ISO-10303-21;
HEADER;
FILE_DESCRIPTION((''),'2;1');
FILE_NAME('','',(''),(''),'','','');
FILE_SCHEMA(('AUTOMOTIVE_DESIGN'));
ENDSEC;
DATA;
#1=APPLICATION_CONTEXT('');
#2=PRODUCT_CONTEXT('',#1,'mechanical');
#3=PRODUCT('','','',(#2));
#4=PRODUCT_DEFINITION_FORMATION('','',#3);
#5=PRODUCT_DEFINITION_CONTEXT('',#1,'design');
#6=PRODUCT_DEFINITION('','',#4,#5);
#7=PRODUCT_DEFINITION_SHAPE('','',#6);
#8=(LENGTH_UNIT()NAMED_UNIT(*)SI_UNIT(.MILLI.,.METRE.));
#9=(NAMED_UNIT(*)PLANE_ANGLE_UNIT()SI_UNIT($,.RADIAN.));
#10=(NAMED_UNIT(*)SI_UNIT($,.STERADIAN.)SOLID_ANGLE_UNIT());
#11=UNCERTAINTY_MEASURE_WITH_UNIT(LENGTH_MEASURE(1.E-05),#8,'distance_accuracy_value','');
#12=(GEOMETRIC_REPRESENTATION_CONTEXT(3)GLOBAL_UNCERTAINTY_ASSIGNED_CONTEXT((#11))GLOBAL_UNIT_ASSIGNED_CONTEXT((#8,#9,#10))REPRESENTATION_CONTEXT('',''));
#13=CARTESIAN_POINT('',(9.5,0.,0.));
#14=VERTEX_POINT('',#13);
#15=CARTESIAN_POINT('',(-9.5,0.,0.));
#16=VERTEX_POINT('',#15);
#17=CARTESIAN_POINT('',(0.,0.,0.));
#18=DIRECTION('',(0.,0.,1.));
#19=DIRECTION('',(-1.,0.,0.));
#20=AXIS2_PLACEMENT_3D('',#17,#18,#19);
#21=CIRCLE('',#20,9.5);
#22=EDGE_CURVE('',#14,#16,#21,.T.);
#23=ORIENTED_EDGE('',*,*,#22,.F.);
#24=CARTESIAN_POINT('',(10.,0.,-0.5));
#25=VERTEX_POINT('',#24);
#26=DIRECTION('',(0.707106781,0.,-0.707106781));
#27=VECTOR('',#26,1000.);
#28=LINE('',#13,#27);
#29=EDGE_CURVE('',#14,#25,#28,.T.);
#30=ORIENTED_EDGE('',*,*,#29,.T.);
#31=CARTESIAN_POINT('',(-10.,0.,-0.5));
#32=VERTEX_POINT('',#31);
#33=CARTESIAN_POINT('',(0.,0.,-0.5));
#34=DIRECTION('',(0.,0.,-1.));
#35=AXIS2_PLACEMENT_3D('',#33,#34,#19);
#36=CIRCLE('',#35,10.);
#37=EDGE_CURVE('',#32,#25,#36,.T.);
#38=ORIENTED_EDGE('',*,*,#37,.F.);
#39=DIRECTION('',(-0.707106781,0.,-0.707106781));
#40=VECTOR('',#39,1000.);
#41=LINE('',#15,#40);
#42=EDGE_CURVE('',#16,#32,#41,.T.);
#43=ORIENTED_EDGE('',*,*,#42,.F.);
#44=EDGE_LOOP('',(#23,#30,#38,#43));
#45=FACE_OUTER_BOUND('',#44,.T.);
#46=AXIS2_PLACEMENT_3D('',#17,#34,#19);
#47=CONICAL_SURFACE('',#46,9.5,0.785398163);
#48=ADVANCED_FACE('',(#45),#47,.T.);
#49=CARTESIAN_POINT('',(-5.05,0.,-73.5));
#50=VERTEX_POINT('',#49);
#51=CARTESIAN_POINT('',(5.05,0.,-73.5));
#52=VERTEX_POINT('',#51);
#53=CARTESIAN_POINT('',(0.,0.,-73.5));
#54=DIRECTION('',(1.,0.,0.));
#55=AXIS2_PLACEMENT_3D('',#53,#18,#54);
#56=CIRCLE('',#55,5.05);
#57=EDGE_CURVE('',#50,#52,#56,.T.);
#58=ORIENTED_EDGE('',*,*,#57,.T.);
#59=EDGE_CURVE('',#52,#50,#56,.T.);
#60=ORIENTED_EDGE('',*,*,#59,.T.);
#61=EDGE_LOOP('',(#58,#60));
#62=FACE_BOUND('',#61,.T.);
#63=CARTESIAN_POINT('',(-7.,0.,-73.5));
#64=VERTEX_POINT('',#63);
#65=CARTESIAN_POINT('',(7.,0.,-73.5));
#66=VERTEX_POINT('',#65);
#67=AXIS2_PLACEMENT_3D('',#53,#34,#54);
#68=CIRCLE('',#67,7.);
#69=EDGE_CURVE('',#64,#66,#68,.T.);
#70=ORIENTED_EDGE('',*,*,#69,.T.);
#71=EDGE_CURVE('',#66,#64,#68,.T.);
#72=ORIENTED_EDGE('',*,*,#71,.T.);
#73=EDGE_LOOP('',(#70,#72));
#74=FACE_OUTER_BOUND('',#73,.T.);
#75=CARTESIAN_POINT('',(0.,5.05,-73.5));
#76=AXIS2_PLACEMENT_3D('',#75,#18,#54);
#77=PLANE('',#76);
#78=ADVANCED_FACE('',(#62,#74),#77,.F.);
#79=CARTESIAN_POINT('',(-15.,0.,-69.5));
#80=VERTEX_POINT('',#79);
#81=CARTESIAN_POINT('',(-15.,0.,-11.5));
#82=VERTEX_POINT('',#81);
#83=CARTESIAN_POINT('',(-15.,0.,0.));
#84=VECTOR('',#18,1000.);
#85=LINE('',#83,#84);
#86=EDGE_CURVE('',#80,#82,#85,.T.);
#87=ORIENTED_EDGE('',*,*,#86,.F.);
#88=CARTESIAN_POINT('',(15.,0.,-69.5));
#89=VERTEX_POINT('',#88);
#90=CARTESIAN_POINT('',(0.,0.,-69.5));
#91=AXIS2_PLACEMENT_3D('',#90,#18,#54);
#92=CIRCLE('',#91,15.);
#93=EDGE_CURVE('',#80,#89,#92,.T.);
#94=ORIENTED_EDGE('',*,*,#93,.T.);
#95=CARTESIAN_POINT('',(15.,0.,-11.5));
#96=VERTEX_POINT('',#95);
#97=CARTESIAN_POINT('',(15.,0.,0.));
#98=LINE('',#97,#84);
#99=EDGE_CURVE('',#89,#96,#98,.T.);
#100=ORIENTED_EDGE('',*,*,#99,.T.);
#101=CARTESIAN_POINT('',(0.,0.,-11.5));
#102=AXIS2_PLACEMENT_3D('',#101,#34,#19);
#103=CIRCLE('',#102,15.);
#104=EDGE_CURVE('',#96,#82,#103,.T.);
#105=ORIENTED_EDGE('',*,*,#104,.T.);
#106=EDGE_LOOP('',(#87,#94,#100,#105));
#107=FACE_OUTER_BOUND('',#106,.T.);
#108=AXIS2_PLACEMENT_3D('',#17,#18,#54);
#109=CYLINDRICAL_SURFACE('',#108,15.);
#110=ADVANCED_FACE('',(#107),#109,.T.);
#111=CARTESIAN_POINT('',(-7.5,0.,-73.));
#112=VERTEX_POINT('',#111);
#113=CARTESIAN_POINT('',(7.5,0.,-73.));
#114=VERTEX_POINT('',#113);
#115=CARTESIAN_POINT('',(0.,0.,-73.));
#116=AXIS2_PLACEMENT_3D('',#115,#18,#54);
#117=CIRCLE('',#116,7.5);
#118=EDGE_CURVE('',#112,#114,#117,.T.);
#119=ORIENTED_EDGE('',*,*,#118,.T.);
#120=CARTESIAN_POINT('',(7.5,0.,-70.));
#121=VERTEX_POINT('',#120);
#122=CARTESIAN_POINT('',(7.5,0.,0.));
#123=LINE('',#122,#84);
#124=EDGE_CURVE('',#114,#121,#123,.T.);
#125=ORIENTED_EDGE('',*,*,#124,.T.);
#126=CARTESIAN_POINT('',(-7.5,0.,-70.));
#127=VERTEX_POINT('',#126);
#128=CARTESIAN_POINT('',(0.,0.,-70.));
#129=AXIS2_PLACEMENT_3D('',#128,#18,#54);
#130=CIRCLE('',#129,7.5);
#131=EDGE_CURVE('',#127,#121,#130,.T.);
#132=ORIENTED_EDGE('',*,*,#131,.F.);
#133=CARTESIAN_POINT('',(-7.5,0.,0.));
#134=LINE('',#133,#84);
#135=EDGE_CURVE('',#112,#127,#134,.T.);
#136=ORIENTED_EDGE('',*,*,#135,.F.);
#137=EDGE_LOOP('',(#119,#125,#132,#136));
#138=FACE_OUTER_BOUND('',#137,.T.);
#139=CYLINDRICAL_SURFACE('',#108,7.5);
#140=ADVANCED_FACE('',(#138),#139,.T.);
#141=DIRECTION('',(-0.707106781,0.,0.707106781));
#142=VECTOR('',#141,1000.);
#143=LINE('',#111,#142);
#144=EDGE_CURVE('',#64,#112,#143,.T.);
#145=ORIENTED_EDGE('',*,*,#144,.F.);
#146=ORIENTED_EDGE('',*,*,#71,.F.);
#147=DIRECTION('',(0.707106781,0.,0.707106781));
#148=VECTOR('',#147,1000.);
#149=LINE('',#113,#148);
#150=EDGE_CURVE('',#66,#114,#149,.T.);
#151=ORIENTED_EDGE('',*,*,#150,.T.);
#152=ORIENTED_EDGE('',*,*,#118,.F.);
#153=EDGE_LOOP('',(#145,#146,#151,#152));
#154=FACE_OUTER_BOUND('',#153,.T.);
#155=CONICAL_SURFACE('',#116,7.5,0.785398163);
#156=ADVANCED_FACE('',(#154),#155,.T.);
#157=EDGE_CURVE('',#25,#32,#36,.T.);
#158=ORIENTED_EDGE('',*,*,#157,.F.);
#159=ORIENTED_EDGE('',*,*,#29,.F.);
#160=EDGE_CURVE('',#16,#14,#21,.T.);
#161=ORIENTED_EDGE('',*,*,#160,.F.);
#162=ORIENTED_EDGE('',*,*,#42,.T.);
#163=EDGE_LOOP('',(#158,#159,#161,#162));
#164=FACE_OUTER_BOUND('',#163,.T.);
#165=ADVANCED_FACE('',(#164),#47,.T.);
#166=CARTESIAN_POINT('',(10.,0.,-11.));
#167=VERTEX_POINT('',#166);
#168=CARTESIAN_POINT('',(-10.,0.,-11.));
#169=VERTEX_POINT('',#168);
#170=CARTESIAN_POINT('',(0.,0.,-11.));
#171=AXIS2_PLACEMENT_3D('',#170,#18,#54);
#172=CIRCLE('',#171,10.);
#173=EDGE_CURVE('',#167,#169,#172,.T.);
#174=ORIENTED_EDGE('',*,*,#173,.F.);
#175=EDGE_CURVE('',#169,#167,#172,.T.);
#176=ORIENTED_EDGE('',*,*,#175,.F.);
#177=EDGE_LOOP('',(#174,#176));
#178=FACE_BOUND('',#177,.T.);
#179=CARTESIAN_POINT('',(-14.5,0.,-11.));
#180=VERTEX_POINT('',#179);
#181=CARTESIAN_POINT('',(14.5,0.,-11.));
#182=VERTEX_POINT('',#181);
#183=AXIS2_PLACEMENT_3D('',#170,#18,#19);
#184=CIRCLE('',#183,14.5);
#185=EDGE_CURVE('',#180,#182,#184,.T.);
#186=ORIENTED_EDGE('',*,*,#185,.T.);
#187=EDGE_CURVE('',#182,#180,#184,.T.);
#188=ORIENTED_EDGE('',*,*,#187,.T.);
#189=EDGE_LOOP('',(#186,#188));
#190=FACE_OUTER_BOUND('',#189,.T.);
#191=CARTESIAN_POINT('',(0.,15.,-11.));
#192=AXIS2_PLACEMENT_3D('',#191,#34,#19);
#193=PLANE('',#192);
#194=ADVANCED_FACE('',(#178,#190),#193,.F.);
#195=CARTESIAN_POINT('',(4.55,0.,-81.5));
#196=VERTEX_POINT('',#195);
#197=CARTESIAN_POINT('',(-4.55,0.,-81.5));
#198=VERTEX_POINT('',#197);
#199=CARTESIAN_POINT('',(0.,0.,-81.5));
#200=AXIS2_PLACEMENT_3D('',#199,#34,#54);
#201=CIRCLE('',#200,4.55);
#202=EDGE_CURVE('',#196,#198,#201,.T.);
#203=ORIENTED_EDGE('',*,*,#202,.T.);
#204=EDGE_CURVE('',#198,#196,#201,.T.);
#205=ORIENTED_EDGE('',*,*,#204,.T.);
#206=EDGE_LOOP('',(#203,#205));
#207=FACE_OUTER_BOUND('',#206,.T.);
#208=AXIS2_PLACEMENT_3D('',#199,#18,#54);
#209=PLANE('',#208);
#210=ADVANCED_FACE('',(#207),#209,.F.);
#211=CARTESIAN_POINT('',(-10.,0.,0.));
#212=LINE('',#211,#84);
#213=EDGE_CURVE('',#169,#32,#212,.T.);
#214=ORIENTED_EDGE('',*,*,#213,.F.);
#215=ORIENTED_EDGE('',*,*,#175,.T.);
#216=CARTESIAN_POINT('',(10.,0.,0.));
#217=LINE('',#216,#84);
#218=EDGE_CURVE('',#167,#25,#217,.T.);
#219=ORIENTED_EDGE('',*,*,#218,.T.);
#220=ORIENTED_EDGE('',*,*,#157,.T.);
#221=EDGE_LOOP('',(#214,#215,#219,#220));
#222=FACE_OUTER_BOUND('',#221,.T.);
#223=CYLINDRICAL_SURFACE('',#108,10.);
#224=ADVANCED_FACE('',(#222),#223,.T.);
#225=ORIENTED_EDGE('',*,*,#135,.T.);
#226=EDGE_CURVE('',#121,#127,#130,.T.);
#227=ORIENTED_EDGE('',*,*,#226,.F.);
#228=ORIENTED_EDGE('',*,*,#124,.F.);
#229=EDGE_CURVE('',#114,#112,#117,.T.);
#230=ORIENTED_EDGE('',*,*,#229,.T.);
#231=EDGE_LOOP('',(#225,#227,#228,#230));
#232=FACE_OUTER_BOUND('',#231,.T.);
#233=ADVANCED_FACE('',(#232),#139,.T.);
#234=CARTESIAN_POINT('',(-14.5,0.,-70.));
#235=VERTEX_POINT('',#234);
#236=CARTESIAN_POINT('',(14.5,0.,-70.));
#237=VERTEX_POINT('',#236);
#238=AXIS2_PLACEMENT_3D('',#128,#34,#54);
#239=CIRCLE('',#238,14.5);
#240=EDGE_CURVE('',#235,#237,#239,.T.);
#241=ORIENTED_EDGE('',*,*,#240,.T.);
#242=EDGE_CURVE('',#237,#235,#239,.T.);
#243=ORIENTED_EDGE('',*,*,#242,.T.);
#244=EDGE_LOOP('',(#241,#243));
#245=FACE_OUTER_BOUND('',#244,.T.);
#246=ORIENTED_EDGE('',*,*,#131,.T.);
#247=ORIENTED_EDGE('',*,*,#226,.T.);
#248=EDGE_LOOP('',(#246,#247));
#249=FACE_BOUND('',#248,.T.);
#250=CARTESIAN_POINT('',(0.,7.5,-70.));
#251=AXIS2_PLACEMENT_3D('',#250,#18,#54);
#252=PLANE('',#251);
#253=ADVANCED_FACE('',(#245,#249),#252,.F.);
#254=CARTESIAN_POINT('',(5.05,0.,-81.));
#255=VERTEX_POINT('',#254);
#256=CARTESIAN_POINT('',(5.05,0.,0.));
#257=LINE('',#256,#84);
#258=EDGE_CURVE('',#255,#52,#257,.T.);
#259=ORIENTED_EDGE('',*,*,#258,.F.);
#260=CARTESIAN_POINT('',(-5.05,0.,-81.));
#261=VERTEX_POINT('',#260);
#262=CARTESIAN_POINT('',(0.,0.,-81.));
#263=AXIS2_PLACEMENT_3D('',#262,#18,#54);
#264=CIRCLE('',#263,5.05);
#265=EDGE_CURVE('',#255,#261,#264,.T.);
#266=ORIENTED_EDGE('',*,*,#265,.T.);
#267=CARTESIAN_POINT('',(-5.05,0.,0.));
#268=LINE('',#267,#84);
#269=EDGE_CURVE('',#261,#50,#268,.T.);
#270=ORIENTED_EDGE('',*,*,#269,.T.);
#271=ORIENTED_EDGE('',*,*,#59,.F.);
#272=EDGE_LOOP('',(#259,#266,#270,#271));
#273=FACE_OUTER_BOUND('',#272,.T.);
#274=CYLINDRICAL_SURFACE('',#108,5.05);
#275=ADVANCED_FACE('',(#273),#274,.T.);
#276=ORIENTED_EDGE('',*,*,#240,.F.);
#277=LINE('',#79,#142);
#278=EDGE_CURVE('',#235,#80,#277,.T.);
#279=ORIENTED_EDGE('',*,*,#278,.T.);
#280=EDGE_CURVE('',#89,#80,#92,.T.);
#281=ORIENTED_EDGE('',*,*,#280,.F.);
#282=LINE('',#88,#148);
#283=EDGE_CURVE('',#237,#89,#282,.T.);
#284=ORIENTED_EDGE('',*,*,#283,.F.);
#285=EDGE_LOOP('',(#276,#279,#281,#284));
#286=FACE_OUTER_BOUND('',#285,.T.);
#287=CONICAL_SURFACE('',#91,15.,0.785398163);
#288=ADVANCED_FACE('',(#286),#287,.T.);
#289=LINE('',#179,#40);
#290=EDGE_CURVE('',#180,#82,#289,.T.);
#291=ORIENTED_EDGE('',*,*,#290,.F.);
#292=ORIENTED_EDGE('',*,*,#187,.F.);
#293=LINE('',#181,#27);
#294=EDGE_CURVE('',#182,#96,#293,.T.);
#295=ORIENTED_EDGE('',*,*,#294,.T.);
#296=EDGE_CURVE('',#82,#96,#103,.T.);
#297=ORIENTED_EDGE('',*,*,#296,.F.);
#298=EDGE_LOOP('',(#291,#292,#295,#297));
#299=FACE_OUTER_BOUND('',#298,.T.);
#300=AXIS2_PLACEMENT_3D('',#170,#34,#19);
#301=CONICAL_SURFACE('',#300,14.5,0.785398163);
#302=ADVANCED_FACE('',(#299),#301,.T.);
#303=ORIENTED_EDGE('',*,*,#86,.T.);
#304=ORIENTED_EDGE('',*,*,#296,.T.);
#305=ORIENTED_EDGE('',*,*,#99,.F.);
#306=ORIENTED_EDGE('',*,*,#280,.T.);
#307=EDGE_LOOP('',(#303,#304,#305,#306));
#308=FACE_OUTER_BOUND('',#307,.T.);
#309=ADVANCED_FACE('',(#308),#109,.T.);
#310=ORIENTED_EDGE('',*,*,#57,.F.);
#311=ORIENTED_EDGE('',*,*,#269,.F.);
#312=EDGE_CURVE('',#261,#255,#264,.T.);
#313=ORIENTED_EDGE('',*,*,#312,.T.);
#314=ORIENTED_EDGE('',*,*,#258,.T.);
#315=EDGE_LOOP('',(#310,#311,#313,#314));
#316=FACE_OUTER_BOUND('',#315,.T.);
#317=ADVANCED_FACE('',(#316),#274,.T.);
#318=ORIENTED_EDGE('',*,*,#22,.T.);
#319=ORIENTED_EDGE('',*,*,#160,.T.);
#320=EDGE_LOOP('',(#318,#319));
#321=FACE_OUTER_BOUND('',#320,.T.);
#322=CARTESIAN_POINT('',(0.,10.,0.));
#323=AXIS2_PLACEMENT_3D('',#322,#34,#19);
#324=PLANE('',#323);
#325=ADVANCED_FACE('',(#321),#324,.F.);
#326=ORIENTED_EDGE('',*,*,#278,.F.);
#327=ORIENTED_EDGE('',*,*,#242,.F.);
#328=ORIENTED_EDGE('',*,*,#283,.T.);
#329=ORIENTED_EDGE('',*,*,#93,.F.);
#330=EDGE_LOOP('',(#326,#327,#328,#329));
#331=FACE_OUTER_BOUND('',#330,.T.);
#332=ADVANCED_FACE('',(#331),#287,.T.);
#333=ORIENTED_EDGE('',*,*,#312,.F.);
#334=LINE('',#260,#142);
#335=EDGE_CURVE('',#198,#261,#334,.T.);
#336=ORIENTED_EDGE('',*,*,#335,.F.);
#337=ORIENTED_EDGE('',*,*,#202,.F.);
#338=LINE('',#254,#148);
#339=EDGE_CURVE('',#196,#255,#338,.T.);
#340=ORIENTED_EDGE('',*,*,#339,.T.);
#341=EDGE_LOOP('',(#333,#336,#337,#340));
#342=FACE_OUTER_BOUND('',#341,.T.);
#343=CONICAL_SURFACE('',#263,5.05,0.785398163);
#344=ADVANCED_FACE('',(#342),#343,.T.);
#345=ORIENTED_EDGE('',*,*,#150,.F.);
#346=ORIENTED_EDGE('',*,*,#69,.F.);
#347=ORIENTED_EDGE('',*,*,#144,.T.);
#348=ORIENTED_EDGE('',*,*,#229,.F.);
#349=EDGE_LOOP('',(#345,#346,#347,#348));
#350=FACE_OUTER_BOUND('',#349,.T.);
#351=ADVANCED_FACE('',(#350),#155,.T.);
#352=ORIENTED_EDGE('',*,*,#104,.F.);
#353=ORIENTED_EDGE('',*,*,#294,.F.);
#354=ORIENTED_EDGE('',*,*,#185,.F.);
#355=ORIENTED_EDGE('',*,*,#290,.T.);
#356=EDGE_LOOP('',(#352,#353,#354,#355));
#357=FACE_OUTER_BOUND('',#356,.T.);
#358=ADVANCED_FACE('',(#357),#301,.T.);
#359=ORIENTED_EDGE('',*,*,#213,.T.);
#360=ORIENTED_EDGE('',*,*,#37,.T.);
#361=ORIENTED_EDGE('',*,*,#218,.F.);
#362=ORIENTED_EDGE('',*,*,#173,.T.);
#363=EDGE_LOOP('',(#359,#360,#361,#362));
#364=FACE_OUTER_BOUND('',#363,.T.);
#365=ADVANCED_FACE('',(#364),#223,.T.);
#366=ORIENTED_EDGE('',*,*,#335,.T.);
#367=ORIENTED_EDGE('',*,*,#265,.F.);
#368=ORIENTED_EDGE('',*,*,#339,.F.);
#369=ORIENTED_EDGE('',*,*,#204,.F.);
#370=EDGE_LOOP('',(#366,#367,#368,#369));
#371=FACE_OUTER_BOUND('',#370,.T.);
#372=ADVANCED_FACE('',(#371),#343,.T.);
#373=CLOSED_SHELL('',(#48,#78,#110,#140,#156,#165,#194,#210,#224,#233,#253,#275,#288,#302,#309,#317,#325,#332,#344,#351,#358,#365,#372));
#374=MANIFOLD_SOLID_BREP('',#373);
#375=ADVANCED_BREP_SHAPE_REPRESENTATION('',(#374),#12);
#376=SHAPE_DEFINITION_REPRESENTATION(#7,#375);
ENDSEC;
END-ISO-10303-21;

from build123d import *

# Parameters (mm, degrees)
CHAMFER1_SIZE = 0.5


with BuildPart() as part:
    # Sketch1 → Revolve1 (revolve)
    with BuildSketch(Plane(origin=(0, 0, 0), x_dir=(0, 0, -1), z_dir=(1, 0, 0)), mode=Mode.PRIVATE) as revolve1_sk:
        Polygon((81.5, 0), (81.5, 5.05), (73.5, 5.05), (73.5, 7.5), (70, 7.5), (70, 15), (11, 15), (11, 10), (0, 10), (0, 0), align=None)
    revolve(revolve1_sk.sketch.rotate(Axis((0, 0, 0), (0, 0, -1)), 90), axis=Axis((0, 0, 0), (0, 0, -1)))

    # Chamfer1
    chamfer1_edges = [part.edges().sort_by_distance(p)[0] for p in [
        (-7.5, 0, -73.5),
        (-5.05, 0, -81.5),
        (-10, 0, 0),
        (-15, 0, -11),
        (-15, 0, -70),
    ]]
    chamfer(chamfer1_edges, length=CHAMFER1_SIZE)


solid = part.part
